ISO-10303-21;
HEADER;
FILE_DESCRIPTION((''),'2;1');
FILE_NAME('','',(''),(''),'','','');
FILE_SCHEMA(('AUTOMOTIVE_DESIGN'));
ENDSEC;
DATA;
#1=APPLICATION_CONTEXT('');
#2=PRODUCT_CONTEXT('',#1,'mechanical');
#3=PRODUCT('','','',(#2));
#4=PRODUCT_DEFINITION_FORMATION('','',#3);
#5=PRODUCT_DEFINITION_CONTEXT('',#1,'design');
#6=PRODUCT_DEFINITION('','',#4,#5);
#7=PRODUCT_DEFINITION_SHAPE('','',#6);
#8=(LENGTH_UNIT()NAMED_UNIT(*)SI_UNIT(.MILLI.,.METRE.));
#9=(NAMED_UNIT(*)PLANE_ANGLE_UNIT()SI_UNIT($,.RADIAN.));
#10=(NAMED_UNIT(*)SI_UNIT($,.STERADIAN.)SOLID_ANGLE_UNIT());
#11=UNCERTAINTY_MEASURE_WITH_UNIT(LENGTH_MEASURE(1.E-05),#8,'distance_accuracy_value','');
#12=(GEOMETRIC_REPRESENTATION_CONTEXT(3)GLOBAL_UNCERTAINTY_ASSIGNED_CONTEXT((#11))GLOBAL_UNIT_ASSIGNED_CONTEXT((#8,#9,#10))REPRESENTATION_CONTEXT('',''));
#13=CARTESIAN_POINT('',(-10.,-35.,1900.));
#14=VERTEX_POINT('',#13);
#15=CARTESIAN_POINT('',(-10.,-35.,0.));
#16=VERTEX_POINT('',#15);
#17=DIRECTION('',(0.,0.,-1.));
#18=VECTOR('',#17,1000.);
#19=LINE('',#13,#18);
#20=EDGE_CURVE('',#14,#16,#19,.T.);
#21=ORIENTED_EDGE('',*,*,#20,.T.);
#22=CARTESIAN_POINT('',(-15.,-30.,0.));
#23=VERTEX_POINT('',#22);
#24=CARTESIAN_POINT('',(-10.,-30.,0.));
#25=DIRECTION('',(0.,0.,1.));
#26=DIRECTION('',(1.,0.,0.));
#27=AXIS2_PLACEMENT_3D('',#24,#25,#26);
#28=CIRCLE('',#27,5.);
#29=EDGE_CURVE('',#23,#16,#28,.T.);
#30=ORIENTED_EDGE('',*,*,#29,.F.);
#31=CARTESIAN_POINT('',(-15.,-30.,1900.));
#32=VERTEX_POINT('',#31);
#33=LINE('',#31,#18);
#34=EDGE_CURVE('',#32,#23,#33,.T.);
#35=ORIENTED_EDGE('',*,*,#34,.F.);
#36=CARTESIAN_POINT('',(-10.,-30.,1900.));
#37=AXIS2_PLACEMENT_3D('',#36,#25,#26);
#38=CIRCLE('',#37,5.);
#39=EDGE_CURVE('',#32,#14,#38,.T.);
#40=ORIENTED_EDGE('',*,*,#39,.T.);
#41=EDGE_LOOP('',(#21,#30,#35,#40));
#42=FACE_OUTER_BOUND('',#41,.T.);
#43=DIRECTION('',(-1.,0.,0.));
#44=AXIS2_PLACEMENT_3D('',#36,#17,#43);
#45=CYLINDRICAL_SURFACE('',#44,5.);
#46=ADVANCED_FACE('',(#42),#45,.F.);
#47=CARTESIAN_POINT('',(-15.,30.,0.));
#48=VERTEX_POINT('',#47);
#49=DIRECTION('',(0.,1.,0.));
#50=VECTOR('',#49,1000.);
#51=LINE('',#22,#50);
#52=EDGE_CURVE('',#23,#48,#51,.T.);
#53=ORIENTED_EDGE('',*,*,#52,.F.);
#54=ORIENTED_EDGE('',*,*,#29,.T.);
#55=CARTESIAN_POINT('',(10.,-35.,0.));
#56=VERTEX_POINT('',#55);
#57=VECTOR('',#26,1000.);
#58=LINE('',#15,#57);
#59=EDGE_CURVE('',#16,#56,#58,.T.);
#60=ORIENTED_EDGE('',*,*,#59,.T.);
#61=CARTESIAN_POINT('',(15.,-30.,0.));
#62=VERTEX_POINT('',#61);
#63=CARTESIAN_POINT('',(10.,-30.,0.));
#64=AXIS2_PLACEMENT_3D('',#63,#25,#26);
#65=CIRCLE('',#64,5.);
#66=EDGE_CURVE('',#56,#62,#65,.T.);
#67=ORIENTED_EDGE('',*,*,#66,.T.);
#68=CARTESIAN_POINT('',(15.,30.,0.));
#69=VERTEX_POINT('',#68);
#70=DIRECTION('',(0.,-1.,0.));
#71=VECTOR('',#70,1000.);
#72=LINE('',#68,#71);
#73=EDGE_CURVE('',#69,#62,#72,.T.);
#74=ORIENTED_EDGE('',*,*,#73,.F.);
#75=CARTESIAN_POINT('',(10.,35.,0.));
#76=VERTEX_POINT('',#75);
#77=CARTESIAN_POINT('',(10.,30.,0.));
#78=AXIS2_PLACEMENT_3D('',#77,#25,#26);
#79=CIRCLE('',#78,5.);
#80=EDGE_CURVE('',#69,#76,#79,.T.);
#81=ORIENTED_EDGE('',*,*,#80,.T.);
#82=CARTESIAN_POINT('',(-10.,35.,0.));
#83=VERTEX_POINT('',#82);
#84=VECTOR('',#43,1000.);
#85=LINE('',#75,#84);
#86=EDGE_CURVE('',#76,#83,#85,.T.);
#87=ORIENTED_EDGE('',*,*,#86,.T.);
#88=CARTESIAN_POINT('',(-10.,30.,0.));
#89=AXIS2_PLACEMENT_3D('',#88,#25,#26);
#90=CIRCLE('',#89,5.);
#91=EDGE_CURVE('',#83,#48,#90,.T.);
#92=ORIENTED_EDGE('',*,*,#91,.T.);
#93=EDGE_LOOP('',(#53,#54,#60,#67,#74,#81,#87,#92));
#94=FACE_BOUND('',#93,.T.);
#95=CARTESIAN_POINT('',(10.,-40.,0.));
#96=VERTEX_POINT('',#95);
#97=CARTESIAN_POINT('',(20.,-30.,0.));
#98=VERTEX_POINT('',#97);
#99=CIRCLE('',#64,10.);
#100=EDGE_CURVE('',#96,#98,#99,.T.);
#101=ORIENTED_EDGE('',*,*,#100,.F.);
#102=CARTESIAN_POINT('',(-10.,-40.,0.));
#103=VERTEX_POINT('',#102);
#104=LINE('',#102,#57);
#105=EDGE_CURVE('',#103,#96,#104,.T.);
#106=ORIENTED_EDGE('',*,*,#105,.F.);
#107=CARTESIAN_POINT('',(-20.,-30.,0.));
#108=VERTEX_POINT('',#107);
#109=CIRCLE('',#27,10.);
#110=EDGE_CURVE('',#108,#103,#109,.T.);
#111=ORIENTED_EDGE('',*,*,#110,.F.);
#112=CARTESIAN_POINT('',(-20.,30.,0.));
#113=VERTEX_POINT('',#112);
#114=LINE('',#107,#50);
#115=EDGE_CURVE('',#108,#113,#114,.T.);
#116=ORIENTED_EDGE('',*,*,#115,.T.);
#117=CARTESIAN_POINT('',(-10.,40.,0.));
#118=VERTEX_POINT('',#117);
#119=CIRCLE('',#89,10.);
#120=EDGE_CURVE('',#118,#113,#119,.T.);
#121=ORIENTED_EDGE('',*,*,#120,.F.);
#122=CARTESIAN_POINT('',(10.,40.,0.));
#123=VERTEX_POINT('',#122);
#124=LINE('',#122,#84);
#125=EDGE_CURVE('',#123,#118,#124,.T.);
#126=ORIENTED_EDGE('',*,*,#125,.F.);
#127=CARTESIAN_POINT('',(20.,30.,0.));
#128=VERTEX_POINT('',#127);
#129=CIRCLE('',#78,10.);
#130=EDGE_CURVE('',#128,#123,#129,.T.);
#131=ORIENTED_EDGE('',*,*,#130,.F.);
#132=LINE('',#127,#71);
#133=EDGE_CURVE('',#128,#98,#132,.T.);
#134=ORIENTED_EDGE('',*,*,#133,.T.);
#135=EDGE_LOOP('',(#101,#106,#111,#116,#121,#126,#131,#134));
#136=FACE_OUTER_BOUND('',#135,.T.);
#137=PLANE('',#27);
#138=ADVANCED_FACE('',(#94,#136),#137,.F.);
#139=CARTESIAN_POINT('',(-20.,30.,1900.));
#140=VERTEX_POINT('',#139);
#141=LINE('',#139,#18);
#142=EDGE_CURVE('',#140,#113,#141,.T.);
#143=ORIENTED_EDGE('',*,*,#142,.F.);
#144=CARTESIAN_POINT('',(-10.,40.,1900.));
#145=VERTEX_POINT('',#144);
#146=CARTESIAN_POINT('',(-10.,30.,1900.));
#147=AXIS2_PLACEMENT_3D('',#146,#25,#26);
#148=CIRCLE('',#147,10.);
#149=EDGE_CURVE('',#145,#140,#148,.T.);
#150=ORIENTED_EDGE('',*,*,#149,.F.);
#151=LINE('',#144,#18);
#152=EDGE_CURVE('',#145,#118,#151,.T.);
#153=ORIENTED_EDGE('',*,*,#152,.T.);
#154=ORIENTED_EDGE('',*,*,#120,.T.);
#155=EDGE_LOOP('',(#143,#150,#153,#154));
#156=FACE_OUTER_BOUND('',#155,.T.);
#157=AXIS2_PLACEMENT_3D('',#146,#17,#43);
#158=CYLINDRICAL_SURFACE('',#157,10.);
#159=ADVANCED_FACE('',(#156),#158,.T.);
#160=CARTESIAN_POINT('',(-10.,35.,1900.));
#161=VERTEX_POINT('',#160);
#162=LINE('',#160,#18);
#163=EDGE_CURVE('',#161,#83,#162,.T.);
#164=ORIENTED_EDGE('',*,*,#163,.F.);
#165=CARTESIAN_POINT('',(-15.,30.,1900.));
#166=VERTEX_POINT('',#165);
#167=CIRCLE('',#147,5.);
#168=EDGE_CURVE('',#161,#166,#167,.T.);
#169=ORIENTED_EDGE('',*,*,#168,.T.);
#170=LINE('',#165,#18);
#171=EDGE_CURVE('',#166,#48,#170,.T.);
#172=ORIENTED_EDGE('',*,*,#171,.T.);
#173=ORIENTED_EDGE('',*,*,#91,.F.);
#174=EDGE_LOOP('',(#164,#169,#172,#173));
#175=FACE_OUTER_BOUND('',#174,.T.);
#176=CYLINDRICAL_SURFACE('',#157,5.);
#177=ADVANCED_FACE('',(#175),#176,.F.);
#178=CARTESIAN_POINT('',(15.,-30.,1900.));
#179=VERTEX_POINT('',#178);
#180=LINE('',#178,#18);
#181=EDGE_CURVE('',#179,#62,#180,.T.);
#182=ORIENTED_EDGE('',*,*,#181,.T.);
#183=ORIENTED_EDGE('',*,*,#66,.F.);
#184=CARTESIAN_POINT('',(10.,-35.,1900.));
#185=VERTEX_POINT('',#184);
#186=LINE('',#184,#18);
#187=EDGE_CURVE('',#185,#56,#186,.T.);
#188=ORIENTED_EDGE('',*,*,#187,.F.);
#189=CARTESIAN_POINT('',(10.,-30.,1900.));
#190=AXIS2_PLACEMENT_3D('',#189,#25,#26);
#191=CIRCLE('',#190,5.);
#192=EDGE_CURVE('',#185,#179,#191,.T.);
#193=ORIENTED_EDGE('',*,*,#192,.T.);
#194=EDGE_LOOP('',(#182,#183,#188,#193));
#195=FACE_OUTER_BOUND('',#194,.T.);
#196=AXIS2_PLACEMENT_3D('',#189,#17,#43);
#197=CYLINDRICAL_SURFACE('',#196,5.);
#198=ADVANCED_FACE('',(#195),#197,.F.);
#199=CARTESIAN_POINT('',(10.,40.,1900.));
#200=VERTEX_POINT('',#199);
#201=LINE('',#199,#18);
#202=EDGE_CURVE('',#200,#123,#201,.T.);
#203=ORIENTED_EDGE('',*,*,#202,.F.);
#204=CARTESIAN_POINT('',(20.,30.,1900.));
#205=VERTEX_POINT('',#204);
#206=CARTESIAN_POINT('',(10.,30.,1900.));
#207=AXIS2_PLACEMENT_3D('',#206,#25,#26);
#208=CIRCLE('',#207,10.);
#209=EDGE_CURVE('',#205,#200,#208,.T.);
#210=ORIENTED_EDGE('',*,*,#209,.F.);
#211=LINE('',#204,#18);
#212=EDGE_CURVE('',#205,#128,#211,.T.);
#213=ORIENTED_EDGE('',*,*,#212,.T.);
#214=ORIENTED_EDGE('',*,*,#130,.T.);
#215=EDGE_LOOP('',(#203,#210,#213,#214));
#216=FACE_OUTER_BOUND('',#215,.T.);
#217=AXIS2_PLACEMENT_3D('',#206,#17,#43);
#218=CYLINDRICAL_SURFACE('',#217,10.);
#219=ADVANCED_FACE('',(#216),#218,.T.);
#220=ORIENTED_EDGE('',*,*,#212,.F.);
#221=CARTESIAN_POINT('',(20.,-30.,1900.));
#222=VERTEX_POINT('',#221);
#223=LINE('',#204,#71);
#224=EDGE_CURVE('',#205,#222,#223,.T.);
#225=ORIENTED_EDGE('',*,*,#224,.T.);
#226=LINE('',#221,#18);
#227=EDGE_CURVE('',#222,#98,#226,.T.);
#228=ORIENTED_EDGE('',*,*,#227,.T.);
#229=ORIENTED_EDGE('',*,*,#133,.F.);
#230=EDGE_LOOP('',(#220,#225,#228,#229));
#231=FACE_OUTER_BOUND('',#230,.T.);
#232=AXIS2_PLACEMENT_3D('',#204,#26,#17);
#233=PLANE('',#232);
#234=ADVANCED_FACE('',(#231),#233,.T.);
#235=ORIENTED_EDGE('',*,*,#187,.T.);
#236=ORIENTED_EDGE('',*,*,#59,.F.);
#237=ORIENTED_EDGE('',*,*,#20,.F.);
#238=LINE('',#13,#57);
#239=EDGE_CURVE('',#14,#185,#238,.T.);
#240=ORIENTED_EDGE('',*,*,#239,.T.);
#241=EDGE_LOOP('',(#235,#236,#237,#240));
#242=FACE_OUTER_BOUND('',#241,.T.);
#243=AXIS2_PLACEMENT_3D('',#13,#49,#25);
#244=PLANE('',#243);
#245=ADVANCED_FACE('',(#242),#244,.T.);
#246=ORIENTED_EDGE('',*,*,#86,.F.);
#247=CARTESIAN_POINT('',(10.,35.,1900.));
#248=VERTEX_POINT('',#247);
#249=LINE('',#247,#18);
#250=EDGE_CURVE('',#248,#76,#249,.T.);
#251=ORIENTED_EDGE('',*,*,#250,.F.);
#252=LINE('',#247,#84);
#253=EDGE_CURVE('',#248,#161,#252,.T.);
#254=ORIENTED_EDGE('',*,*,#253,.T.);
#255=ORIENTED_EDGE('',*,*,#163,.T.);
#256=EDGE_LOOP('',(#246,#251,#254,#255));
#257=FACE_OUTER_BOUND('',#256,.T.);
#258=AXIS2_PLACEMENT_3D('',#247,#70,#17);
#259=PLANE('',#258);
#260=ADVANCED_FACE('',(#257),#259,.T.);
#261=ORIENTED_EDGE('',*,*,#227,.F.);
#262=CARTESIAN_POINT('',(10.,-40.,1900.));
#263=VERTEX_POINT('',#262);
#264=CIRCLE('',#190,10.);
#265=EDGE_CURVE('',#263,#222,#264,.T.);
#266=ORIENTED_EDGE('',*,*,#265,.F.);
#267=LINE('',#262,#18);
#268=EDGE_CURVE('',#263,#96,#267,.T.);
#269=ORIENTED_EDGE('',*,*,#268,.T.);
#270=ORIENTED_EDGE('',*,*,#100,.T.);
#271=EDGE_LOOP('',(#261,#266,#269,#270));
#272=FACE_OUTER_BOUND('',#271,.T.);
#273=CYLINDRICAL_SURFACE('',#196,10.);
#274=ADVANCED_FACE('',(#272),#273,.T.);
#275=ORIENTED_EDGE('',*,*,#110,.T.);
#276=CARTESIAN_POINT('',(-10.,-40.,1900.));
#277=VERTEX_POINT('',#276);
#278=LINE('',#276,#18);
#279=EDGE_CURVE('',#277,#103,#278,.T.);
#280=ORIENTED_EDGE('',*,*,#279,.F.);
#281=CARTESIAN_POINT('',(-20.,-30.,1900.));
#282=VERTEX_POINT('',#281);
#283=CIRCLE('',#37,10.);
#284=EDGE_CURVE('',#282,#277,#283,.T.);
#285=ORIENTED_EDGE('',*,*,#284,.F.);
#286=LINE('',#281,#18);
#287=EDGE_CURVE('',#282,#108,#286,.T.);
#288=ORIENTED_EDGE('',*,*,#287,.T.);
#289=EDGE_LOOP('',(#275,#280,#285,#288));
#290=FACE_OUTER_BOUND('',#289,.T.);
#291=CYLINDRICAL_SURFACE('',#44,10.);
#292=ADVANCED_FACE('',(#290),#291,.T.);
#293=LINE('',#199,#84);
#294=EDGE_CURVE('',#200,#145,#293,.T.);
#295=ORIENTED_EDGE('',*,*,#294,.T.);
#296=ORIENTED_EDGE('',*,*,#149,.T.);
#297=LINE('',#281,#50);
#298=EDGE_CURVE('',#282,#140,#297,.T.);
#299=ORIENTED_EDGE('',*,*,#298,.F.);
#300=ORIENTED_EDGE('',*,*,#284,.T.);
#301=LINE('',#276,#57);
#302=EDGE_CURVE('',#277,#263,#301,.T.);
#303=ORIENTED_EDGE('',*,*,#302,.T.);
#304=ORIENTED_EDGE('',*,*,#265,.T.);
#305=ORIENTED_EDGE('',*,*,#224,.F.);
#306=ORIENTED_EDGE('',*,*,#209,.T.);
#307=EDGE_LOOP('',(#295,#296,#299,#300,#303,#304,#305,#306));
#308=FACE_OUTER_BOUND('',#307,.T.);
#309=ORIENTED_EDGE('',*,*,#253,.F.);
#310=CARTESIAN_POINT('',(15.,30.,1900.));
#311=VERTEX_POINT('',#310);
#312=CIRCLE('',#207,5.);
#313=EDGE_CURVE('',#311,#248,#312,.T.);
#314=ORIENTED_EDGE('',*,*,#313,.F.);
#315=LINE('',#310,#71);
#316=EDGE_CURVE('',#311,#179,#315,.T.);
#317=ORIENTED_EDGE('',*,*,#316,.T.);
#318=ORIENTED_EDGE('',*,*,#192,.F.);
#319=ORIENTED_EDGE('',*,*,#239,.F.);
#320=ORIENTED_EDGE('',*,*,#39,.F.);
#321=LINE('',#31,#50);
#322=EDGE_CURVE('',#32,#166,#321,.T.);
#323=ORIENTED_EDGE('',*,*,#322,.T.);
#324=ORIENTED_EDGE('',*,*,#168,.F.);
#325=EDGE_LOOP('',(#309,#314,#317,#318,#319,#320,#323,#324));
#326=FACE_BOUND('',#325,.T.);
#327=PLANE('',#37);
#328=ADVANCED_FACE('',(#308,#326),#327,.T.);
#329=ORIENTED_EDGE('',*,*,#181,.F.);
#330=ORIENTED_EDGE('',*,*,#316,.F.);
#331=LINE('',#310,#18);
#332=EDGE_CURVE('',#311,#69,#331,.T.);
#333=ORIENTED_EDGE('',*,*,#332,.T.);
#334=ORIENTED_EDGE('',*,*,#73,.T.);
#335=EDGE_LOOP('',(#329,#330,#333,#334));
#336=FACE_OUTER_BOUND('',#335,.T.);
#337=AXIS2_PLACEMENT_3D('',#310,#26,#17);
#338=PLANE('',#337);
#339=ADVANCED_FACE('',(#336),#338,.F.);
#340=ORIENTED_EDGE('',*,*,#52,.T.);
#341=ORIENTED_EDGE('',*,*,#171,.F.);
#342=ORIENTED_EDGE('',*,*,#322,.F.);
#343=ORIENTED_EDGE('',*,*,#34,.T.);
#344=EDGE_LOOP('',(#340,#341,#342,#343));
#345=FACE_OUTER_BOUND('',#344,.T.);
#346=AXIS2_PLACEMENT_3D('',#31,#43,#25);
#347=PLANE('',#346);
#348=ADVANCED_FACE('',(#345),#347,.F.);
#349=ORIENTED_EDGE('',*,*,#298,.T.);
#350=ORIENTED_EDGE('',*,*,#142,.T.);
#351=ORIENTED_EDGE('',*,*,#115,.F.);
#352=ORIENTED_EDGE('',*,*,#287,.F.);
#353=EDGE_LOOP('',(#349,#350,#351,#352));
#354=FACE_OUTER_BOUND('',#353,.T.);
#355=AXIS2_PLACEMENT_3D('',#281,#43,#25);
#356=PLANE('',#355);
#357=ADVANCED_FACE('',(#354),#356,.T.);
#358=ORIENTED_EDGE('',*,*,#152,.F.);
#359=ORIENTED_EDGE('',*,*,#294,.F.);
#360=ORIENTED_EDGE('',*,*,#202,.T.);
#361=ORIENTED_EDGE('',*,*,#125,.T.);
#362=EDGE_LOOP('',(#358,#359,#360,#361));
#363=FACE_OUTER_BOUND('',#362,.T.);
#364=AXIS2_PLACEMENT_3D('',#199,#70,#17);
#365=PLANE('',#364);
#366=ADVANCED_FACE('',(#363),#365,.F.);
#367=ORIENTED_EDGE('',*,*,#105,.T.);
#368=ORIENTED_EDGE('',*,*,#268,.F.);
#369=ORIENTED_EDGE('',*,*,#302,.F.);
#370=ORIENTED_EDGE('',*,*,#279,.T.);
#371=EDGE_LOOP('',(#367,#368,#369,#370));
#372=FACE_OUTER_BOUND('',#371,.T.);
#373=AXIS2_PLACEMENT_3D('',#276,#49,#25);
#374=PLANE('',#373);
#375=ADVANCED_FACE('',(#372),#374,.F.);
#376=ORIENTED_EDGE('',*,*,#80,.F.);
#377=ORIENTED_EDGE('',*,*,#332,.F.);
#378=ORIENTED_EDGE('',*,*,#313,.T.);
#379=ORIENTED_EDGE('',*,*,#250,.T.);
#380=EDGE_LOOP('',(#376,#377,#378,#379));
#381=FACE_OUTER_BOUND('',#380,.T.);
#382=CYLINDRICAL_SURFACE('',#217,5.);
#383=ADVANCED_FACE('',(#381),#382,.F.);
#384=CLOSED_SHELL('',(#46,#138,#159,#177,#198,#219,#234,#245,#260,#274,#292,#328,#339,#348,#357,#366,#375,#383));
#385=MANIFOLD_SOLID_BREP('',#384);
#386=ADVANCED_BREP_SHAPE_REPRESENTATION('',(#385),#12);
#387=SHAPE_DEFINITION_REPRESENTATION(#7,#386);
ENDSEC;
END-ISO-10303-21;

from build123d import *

# Parameters (mm, degrees)
BOSS_EXTRUDE1_DEPTH = 1900


with BuildPart() as part:
    # Sketch1 → Boss-Extrude1 (new body)
    with BuildSketch(Plane.XY):
        with BuildLine():
            Line((-10, -40), (10, -40))
            ThreePointArc((10, -40), (17.071067812, -37.071067812), (20, -30))
            Line((20, -30), (20, 30))
            ThreePointArc((20, 30), (17.071067812, 37.071067812), (10, 40))
            Line((10, 40), (-10, 40))
            ThreePointArc((-10, 40), (-17.071067812, 37.071067812), (-20, 30))
            Line((-20, 30), (-20, -30))
            ThreePointArc((-20, -30), (-17.071067812, -37.071067812), (-10, -40))
        make_face()
        with BuildLine():
            Line((-10, -35), (10, -35))
            ThreePointArc((10, -35), (13.535533906, -33.535533906), (15, -30))
            Line((15, -30), (15, 30))
            ThreePointArc((15, 30), (13.535533906, 33.535533906), (10, 35))
            Line((10, 35), (-10, 35))
            ThreePointArc((-10, 35), (-13.535533906, 33.535533906), (-15, 30))
            Line((-15, 30), (-15, -30))
            ThreePointArc((-15, -30), (-13.535533906, -33.535533906), (-10, -35))
        make_face(mode=Mode.SUBTRACT)
    extrude(amount=BOSS_EXTRUDE1_DEPTH)


solid = part.part
